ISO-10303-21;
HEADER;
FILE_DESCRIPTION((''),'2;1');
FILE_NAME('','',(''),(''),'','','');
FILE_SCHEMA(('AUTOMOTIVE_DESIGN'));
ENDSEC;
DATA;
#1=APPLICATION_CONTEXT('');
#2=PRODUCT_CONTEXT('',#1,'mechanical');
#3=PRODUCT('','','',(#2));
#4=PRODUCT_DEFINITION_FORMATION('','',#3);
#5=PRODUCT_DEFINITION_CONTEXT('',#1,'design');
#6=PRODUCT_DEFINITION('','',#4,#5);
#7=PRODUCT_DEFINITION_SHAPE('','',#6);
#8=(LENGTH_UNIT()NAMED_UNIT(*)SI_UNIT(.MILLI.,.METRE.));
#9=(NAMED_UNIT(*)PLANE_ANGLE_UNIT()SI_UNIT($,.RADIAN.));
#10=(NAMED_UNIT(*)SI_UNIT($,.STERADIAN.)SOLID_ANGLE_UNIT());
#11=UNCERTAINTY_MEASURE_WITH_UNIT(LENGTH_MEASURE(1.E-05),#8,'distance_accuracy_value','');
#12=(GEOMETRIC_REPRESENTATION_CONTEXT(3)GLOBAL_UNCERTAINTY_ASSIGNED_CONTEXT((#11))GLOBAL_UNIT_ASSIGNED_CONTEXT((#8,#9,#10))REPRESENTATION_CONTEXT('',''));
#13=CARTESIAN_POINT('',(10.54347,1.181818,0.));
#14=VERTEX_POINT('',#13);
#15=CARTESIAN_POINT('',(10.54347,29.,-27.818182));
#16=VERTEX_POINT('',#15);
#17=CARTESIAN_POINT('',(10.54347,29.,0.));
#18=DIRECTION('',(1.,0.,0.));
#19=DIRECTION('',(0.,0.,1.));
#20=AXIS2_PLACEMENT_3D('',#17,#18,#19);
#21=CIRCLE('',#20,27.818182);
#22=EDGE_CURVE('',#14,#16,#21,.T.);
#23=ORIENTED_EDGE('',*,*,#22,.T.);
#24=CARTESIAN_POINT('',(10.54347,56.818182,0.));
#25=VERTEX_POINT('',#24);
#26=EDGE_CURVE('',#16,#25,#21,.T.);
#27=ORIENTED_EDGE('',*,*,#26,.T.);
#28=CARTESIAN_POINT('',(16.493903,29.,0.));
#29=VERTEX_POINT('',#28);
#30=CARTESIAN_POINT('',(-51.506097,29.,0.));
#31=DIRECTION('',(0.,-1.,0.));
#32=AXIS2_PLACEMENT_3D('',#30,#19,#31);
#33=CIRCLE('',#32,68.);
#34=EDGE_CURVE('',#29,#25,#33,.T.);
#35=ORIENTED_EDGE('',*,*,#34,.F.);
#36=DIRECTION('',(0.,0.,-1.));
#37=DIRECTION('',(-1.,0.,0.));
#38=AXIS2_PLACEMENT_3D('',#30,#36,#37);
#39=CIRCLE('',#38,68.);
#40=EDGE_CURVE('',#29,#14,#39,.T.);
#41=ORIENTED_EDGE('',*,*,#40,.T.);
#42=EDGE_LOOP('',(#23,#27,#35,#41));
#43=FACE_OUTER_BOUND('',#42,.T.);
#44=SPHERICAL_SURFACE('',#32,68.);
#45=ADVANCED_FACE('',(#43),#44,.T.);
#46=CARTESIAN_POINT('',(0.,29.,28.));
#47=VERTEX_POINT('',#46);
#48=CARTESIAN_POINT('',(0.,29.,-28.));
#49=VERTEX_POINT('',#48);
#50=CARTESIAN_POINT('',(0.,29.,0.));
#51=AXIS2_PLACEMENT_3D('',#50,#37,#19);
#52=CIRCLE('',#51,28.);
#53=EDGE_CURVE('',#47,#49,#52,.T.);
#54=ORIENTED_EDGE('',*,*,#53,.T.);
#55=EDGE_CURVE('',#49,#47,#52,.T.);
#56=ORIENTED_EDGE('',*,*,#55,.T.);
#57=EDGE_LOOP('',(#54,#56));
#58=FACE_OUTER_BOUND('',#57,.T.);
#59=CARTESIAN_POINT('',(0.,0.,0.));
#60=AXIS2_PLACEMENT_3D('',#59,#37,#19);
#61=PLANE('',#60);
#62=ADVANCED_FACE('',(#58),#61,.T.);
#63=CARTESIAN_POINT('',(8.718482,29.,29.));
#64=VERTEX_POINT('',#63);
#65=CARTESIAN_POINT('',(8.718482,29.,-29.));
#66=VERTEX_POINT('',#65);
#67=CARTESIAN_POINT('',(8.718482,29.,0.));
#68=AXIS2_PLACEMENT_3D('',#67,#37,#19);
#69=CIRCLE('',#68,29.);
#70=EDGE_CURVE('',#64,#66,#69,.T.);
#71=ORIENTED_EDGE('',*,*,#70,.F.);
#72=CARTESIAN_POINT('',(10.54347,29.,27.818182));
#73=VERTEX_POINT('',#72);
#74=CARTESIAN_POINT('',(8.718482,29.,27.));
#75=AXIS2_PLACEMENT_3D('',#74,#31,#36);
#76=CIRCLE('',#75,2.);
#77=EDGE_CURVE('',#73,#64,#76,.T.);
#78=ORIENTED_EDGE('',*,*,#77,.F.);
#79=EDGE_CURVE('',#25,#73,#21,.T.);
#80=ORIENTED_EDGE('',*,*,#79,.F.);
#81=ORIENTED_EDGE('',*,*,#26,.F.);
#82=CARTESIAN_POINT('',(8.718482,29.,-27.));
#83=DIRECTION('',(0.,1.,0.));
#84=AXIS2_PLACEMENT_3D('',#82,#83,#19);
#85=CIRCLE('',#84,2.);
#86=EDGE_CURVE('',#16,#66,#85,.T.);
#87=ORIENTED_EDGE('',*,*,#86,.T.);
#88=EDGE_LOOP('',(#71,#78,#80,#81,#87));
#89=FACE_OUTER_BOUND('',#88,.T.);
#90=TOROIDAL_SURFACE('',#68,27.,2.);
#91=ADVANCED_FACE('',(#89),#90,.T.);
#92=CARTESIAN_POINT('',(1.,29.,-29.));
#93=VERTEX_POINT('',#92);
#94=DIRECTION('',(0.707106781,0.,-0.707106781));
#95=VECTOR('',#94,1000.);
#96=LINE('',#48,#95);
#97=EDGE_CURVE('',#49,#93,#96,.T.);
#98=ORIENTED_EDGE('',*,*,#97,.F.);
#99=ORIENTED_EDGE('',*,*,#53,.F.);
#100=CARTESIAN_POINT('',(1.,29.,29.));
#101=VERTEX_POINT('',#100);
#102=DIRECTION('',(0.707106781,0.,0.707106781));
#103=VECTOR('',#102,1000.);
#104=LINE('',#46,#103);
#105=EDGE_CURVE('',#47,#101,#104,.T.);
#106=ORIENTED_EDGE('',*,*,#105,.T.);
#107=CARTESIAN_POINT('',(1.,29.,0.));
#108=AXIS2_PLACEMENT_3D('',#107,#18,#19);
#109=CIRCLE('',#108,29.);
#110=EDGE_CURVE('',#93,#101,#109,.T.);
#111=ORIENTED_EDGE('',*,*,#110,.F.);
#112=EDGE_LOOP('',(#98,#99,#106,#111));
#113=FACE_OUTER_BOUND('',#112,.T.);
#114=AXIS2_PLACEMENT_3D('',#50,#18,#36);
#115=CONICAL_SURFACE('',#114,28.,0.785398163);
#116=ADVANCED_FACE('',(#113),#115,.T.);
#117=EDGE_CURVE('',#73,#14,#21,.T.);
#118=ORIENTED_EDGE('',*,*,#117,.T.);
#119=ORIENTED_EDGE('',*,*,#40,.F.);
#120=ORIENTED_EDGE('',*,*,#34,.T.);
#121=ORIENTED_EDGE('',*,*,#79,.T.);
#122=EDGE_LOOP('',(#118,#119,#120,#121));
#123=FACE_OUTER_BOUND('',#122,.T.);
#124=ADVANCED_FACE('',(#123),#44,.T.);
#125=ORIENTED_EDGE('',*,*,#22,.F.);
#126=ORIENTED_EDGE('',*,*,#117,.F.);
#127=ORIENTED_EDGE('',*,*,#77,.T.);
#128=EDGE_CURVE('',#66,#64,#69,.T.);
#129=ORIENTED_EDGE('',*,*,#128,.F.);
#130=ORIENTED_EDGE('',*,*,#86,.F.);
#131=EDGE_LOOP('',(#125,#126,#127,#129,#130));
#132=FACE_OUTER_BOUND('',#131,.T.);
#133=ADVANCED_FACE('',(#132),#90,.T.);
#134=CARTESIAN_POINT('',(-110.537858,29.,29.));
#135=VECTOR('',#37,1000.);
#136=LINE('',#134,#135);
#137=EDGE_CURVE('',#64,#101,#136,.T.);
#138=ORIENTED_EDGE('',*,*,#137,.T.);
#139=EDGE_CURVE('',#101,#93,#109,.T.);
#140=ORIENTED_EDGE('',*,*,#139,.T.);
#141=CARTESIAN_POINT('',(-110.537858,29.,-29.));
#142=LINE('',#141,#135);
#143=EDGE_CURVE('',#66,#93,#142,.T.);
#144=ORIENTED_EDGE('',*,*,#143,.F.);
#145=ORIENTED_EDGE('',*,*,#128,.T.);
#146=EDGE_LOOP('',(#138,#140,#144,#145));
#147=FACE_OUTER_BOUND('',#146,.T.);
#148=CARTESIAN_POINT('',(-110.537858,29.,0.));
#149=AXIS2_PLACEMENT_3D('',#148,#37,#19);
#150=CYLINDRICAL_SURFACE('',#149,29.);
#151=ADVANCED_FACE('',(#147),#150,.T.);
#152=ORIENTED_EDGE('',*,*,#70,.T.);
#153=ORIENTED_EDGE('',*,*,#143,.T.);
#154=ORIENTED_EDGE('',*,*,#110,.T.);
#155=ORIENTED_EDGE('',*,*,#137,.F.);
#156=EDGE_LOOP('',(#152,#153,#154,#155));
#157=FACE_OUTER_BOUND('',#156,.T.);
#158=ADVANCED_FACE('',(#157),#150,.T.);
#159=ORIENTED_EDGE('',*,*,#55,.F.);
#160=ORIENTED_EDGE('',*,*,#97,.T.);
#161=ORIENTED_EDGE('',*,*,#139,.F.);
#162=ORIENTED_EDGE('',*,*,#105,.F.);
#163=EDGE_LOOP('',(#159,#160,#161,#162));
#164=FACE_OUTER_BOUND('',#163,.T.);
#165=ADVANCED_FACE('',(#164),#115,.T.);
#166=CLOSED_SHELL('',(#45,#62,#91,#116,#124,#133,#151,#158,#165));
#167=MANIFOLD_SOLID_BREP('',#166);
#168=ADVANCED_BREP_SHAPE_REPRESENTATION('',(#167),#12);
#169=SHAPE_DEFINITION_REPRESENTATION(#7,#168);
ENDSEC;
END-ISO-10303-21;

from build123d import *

# Parameters (mm, degrees)
FILLET2_R     = 2
CHAMFER1_SIZE = 1


with BuildPart() as part:
    # Sketch1 → Revolve1 (revolve)
    with BuildSketch(Plane.XY, mode=Mode.PRIVATE) as revolve1_sk:
        with BuildLine():
            Line((0, 0), (10, 0))
            ThreePointArc((10, 0), (14.850570129, 14.140905371), (16.493902741, 29))
            Line((16.493902741, 29), (0, 29))
            Line((0, 29), (0, 0))
        make_face()
    revolve(revolve1_sk.sketch.rotate(Axis((-110.537857647, 29, 0), (1, 0, 0)), 270), axis=Axis((-110.537857647, 29, 0), (1, 0, 0)))

    # Fillet2
    fillet2_edges = [part.edges().sort_by_distance(p)[0] for p in [
        (10, 29, -29),
    ]]
    fillet(fillet2_edges, radius=FILLET2_R)

    # Chamfer1
    chamfer1_edges = [part.edges().sort_by_distance(p)[0] for p in [
        (0, 29, -29),
    ]]
    chamfer(chamfer1_edges, length=CHAMFER1_SIZE)


solid = part.part
